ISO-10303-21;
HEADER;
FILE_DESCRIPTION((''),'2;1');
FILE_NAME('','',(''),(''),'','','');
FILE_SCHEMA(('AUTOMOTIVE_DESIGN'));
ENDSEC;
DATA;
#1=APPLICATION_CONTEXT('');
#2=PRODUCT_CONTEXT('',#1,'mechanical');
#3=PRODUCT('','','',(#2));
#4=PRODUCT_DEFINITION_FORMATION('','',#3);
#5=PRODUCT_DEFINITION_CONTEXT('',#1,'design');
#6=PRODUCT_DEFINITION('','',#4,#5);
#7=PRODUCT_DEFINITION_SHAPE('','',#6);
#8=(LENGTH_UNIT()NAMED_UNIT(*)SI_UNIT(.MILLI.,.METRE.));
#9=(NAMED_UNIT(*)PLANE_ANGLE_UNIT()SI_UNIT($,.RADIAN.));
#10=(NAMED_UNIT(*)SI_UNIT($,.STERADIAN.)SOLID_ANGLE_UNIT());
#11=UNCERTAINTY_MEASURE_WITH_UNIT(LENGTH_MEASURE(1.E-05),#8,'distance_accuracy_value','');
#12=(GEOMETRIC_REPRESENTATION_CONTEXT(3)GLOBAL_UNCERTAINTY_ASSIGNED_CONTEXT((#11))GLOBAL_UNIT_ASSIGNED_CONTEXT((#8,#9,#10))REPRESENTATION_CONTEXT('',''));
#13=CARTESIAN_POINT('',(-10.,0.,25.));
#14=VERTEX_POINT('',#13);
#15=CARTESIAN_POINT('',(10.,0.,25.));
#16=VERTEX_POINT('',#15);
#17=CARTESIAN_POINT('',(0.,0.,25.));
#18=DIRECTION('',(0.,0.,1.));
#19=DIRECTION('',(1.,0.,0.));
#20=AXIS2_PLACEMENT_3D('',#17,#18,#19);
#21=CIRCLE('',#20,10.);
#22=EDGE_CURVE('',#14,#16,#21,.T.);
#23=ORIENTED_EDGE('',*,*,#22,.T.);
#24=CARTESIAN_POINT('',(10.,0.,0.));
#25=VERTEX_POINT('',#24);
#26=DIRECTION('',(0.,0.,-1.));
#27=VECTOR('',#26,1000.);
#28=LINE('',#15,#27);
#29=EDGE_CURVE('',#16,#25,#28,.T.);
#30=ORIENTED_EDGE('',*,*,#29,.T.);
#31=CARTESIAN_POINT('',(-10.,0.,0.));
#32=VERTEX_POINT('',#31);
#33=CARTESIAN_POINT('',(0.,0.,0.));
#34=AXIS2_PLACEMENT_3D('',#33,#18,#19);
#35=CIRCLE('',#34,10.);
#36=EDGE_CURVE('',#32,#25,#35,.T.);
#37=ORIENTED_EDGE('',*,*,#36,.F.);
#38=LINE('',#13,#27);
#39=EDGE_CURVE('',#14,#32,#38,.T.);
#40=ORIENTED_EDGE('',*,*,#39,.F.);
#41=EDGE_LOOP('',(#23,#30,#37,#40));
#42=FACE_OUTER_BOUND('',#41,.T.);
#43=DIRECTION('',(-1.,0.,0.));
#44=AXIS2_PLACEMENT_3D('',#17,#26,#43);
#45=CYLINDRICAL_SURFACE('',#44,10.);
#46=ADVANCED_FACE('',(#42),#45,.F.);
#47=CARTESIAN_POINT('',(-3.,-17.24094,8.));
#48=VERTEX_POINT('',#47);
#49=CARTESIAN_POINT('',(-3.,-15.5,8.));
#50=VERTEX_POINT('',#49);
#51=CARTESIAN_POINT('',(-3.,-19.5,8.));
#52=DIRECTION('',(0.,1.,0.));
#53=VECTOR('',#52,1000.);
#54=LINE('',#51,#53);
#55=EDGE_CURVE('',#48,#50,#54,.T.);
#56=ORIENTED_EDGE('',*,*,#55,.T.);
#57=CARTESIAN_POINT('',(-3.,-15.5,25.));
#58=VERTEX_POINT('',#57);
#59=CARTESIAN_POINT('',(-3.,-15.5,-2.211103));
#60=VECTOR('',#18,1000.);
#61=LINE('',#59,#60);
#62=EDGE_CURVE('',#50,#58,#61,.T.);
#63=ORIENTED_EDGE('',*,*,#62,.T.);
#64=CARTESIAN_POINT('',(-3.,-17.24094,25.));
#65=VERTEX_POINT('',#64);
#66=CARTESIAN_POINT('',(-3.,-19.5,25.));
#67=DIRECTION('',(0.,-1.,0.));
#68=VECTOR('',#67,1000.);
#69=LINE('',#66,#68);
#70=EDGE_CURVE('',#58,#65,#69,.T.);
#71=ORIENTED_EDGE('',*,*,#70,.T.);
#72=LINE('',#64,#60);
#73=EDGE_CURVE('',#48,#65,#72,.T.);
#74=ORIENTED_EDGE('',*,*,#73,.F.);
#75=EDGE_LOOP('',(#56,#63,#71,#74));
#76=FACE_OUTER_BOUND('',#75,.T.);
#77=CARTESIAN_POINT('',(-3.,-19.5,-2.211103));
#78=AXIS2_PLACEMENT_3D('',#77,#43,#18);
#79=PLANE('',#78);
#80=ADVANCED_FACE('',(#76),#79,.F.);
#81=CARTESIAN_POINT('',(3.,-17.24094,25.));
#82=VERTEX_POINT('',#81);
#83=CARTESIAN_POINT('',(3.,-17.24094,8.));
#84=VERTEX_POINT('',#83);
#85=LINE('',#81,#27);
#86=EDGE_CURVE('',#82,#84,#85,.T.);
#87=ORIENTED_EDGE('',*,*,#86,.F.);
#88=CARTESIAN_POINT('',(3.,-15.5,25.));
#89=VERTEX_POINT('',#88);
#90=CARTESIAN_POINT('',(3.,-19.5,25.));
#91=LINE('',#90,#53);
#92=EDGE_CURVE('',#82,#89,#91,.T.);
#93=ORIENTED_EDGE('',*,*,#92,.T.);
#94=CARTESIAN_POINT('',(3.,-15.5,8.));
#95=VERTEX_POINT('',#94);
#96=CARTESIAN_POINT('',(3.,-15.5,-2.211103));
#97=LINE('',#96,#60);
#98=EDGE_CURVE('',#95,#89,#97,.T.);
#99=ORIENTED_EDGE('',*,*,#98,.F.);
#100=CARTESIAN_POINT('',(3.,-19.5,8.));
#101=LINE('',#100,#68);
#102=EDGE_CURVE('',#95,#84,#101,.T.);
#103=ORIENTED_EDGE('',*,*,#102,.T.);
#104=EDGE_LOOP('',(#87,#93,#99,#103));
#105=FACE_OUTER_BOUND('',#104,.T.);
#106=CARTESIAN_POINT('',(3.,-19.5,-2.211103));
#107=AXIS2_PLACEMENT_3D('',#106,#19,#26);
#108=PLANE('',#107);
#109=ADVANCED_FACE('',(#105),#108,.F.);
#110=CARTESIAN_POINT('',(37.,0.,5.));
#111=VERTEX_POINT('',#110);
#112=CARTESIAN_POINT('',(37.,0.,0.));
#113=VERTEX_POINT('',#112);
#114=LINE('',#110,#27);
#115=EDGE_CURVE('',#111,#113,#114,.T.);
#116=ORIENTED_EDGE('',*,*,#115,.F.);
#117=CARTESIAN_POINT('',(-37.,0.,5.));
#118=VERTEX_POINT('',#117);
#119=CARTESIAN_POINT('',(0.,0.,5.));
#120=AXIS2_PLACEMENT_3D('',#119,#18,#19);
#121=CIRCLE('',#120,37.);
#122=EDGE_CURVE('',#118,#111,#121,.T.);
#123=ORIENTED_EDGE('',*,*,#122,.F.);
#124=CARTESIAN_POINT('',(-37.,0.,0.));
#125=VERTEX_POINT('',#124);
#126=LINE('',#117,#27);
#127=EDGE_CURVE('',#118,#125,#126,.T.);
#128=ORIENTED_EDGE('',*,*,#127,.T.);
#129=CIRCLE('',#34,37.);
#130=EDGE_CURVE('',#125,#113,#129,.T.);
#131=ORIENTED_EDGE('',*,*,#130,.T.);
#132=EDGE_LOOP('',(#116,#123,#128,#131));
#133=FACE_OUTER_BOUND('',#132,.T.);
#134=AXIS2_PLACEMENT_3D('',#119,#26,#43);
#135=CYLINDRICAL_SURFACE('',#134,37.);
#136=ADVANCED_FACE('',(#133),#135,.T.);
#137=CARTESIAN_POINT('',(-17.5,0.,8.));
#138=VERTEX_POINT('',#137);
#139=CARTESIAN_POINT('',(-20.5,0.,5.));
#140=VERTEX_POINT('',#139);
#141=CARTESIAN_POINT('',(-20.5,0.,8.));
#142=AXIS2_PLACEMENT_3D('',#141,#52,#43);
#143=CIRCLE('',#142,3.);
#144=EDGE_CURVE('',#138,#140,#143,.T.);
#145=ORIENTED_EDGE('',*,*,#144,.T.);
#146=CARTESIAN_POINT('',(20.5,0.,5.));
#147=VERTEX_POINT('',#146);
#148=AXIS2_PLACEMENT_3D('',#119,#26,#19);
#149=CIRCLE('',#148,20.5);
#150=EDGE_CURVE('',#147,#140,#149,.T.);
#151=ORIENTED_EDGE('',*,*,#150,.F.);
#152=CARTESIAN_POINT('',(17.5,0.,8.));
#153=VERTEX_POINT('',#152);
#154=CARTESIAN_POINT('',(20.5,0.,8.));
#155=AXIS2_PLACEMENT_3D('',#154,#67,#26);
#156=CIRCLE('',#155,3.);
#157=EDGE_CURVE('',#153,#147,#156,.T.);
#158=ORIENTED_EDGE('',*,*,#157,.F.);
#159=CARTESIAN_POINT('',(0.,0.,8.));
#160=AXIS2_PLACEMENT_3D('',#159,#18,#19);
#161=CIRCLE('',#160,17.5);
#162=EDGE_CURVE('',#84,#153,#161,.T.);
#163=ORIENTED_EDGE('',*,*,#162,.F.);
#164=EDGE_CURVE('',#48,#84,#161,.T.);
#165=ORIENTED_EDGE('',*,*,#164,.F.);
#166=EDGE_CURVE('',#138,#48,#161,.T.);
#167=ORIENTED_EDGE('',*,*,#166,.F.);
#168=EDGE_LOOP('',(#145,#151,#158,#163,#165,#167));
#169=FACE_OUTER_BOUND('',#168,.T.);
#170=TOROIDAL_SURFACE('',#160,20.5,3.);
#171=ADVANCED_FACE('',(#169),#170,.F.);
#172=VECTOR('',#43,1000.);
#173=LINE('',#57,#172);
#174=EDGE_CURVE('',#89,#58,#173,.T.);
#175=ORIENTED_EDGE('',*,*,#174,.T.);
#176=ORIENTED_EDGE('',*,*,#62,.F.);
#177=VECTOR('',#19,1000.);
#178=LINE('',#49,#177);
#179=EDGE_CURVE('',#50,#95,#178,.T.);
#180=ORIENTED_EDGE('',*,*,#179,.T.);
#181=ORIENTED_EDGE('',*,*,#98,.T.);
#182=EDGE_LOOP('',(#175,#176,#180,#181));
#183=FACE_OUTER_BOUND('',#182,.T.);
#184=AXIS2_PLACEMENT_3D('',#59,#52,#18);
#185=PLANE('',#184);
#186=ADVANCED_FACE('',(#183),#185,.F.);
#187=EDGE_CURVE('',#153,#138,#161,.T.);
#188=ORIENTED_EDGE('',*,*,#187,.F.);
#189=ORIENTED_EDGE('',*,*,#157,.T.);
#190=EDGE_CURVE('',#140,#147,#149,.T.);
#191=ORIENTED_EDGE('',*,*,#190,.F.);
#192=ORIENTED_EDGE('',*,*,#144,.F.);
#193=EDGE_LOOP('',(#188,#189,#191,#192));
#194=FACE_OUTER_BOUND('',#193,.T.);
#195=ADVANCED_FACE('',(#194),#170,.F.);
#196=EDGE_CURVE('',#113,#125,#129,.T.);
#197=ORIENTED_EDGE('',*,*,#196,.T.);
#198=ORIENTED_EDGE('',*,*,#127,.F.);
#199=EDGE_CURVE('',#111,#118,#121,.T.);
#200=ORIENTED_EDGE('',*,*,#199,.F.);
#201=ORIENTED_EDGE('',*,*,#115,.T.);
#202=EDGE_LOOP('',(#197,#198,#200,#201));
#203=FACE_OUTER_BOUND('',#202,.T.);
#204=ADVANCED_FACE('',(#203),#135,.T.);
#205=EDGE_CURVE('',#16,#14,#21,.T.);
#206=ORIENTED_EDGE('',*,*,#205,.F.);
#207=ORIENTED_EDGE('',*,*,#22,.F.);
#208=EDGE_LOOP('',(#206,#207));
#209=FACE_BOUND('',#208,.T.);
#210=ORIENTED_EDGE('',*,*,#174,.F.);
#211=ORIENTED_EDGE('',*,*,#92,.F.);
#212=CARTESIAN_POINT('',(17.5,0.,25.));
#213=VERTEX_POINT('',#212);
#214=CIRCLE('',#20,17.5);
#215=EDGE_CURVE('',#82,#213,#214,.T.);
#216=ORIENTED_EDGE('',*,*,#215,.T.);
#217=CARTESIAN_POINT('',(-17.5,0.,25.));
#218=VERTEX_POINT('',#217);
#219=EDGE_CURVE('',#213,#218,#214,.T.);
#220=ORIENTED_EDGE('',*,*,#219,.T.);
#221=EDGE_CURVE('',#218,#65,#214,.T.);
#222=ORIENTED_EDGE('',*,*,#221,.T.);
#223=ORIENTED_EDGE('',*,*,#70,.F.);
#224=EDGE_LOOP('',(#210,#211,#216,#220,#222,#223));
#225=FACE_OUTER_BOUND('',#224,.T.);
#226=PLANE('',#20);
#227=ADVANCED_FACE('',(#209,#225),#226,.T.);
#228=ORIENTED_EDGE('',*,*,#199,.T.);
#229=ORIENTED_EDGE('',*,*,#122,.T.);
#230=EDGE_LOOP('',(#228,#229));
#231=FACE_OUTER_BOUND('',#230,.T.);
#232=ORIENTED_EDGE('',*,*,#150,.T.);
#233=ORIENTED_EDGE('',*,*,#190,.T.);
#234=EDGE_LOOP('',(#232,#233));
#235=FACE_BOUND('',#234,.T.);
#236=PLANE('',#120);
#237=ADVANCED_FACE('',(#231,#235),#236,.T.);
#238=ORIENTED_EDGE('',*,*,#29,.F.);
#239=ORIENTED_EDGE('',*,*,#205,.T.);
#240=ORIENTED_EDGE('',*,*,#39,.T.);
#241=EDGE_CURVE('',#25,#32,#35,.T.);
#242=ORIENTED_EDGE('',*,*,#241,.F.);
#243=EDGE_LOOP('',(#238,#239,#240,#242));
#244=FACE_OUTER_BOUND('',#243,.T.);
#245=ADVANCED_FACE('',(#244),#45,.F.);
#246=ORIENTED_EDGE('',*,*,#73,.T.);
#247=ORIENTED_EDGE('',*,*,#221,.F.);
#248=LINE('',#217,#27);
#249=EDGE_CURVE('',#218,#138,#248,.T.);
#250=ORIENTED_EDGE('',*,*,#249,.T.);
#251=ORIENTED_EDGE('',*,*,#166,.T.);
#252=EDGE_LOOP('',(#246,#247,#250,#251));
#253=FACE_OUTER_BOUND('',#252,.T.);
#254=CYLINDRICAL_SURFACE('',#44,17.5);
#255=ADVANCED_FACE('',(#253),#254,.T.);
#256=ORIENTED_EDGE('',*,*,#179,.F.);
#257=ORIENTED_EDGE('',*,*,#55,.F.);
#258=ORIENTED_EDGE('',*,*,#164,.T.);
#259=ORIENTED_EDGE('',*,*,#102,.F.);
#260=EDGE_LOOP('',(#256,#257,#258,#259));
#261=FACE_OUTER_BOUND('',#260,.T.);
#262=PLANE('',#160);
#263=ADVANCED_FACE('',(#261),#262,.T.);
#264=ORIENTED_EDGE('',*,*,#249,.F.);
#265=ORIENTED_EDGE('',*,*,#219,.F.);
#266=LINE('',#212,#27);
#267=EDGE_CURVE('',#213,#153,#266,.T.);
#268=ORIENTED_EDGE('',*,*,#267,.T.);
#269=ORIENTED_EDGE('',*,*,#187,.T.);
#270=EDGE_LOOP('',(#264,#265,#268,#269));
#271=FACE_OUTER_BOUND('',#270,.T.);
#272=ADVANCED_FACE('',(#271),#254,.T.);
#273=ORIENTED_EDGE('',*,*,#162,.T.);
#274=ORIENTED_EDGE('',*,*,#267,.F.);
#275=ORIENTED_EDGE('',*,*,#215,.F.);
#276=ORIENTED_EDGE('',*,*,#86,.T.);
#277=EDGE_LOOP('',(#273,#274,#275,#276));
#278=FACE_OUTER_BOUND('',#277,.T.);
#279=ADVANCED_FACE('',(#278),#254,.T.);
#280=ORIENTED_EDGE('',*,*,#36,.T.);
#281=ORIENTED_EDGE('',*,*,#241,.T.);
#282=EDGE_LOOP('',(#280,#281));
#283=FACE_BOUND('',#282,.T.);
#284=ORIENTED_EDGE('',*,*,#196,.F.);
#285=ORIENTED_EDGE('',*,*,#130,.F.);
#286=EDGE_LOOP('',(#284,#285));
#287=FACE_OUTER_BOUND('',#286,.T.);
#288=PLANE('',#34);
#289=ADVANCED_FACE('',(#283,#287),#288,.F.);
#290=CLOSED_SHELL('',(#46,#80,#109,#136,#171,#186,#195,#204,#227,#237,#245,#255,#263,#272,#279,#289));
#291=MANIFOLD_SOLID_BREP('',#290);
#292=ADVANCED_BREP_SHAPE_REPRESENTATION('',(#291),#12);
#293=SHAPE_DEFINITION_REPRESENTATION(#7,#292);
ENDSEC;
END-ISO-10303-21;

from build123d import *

# Parameters (mm, degrees)
SKETCH1_R           = 37
BOSS_EXTRUDE1_DEPTH = 5
SKETCH2_R           = 17.5
SKETCH2_R_2         = 10
BOSS_EXTRUDE2_DEPTH = 20
SKETCH3_R           = 10
CUT_EXTRUDE1_DEPTH  = 58.99137867
FILLET1_R           = 3
SKETCH4_W           = 6
SKETCH4_H           = 4
CUT_EXTRUDE2_DEPTH  = 17


with BuildPart() as part:
    # Sketch1 → Boss-Extrude1 (new body)
    with BuildSketch(Plane.XY):
        Circle(SKETCH1_R)
    extrude(amount=BOSS_EXTRUDE1_DEPTH)

    # Sketch2 → Boss-Extrude2 (add)
    with BuildSketch(Plane.XY.offset(5)):
        Circle(SKETCH2_R)
        Circle(SKETCH2_R_2, mode=Mode.SUBTRACT)
    extrude(amount=BOSS_EXTRUDE2_DEPTH)

    # Sketch3 → Cut-Extrude1 (cut, through all)
    with BuildSketch(Plane.XY.offset(25)):
        Circle(SKETCH3_R)
    extrude(amount=-CUT_EXTRUDE1_DEPTH, mode=Mode.SUBTRACT)

    # Fillet1
    fillet1_edges = [part.edges().sort_by_distance(p)[0] for p in [
        (-17.5, 0, 5),
    ]]
    fillet(fillet1_edges, radius=FILLET1_R)

    # Sketch4 → Cut-Extrude2 (cut)
    with BuildSketch(Plane.XY.offset(25)):
        with Locations((0, -17.5)):
            Rectangle(SKETCH4_W, SKETCH4_H)
    extrude(amount=-CUT_EXTRUDE2_DEPTH, mode=Mode.SUBTRACT)


solid = part.part
